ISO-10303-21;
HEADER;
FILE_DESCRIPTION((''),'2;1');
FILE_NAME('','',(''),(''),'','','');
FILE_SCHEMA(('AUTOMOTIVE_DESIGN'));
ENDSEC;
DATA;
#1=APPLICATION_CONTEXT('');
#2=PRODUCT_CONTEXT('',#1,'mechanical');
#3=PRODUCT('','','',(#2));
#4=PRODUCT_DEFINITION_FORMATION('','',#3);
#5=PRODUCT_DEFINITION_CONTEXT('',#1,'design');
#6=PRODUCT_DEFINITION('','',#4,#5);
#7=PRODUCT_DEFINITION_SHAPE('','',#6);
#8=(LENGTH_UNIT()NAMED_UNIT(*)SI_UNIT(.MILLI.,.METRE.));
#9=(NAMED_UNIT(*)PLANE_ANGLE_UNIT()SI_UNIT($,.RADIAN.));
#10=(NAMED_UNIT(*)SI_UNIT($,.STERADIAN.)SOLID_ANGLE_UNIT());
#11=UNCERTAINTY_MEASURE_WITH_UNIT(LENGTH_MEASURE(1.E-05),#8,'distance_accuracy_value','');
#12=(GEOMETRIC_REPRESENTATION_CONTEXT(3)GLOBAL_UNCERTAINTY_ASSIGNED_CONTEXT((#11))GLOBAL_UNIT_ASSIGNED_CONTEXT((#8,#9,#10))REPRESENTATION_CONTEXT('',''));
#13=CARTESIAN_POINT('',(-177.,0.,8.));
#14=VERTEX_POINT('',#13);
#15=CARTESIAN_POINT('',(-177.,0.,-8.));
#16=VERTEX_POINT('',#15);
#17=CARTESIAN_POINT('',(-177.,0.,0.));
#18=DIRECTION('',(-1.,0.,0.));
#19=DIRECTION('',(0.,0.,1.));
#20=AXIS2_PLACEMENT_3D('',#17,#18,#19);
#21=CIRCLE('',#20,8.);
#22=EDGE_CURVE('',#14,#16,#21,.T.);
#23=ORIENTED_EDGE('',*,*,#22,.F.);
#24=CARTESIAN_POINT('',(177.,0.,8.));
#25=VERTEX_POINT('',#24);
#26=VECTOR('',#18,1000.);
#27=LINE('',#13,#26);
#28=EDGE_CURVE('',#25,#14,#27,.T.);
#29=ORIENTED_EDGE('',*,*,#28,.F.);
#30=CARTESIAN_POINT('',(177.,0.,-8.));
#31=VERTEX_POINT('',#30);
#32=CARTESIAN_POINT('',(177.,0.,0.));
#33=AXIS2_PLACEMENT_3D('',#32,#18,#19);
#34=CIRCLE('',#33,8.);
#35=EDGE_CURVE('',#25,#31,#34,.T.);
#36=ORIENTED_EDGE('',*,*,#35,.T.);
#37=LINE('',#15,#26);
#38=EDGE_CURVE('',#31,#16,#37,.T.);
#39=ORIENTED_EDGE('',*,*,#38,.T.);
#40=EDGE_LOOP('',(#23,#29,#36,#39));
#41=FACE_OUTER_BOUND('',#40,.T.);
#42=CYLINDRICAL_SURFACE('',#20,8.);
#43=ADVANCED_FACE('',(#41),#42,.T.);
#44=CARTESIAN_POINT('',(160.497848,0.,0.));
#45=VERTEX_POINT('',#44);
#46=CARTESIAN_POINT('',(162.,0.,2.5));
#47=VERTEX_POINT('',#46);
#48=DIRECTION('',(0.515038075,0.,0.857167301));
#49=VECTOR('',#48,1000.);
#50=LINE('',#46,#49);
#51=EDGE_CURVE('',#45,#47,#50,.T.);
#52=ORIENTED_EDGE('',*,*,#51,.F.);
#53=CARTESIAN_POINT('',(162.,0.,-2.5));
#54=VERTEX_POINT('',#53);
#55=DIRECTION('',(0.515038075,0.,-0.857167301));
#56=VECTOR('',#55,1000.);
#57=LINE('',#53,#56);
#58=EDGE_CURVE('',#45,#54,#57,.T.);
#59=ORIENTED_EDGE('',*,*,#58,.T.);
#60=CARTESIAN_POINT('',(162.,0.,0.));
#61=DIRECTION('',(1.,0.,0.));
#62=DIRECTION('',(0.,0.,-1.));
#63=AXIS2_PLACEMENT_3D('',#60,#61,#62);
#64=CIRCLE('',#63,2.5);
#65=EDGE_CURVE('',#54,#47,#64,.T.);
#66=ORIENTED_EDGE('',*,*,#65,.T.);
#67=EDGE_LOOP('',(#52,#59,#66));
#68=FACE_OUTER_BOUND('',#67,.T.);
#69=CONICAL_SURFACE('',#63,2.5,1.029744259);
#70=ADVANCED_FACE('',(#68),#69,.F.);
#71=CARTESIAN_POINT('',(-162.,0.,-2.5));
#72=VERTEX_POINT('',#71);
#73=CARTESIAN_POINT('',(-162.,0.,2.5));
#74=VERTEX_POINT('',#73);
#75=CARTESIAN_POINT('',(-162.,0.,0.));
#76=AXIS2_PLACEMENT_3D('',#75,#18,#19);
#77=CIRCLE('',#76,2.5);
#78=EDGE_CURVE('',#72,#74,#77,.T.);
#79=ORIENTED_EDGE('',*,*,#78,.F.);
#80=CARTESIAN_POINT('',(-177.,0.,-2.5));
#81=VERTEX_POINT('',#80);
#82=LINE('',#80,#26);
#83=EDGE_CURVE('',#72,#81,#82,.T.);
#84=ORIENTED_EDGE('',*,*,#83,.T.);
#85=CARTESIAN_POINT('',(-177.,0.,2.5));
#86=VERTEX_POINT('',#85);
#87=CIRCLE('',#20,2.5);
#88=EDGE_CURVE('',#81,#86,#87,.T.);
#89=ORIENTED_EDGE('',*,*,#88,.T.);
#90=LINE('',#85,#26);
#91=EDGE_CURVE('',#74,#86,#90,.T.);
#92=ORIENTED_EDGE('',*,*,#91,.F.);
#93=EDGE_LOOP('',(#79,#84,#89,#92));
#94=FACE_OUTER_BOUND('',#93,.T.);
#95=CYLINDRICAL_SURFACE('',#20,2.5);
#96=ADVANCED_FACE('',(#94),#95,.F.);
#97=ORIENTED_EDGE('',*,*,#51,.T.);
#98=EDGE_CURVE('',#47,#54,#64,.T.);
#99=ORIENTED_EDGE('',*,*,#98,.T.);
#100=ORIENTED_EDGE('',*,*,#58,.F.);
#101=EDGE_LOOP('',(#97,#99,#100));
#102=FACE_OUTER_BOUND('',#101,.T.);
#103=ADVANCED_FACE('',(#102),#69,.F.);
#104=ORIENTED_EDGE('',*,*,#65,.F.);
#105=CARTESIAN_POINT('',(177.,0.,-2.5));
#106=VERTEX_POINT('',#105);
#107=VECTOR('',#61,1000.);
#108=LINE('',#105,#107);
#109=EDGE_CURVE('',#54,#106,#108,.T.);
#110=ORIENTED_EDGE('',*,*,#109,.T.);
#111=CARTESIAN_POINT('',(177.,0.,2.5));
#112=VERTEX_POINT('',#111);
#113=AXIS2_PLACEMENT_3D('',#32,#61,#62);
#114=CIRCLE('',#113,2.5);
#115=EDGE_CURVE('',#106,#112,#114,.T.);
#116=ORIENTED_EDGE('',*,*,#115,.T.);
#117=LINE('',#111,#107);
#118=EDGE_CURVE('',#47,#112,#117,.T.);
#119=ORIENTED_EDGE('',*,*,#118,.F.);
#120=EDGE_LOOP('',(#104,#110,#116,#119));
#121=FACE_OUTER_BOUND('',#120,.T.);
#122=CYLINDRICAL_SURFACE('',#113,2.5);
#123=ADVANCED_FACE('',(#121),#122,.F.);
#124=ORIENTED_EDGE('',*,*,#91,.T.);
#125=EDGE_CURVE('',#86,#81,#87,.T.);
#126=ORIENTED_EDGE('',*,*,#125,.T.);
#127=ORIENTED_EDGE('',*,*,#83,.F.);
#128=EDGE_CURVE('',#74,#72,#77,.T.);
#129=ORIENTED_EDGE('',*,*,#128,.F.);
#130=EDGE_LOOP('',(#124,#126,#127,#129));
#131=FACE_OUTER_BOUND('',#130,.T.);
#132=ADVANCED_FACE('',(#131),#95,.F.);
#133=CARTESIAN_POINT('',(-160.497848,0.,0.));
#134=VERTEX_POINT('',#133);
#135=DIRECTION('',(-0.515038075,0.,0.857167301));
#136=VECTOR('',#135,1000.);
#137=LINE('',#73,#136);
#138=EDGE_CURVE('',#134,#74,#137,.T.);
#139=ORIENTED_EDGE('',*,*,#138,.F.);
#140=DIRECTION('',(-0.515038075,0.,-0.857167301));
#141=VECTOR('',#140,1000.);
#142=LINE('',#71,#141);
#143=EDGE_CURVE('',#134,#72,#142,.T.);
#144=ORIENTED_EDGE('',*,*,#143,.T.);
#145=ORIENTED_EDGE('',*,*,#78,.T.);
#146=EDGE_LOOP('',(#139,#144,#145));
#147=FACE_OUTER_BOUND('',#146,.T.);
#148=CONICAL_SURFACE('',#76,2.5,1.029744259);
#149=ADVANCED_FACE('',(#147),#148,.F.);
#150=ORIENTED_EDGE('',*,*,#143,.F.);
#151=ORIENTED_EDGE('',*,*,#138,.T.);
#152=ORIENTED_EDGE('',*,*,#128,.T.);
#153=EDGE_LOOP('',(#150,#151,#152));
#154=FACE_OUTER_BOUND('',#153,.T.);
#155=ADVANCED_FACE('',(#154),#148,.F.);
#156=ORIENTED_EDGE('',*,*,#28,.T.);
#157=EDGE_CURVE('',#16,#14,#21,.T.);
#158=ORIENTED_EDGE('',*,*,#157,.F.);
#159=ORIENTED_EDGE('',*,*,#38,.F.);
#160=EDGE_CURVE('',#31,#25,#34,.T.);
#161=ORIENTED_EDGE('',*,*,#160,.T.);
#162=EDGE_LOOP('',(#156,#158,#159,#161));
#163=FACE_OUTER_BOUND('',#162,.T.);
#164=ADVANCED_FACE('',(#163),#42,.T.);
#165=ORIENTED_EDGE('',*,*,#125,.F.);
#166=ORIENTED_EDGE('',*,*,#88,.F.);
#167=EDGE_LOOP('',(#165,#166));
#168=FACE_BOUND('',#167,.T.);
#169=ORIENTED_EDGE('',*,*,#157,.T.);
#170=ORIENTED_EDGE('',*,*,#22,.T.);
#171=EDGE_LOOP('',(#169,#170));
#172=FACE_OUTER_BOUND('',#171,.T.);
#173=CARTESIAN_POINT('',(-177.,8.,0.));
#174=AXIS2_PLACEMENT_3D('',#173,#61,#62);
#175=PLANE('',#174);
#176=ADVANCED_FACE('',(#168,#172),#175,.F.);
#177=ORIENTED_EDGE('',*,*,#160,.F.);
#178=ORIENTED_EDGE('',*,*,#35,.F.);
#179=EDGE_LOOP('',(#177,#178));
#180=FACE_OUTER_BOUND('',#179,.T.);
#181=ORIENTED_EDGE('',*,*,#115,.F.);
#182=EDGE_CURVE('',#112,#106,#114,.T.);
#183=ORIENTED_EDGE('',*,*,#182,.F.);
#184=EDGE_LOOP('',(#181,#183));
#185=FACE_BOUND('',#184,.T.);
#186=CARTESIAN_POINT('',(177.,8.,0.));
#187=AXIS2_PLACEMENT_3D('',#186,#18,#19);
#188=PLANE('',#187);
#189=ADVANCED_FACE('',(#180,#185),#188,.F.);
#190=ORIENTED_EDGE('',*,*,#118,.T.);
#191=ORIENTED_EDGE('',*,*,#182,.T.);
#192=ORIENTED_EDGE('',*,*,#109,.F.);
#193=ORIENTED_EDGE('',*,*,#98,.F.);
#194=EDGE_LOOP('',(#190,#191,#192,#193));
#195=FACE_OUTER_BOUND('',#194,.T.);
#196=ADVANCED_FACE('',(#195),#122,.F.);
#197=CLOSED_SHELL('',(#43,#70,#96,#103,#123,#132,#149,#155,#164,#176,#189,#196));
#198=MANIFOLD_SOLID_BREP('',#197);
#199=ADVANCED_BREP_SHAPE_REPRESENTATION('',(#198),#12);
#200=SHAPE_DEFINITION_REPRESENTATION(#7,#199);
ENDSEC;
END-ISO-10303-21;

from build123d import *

# Parameters (mm, degrees)
SKETCH1_W             = 354
SKETCH1_H             = 8
M6_TAPPED_HOLE1_D     = 5
M6_TAPPED_HOLE1_DEPTH = 15
M6_TAPPED_HOLE1_TIP   = 1.502151548
M6_TAPPED_HOLE2_D     = 5
M6_TAPPED_HOLE2_DEPTH = 15
M6_TAPPED_HOLE2_TIP   = 1.502151548


with BuildPart() as part:
    # Sketch1 → Revolve1 (revolve)
    with BuildSketch(Plane.XY, mode=Mode.PRIVATE) as revolve1_sk:
        with Locations((0, 4)):
            Rectangle(SKETCH1_W, SKETCH1_H)
    revolve(revolve1_sk.sketch.rotate(Axis((-177, 0, 0), (1, 0, 0)), 90), axis=Axis((-177, 0, 0), (1, 0, 0)))

    # M6 Tapped Hole1
    with Locations(Plane(origin=(177, 0, 0), x_dir=(0, 0, -1), z_dir=(1, 0, 0))):
        with Locations((0, 0)):
            Hole(M6_TAPPED_HOLE1_D / 2, depth=M6_TAPPED_HOLE1_DEPTH)
            with Locations((0, 0, -(M6_TAPPED_HOLE1_DEPTH + M6_TAPPED_HOLE1_TIP / 2))):  # 118° drill point
                Cone(0, M6_TAPPED_HOLE1_D / 2, M6_TAPPED_HOLE1_TIP, mode=Mode.SUBTRACT)

    # M6 Tapped Hole2
    with Locations(Plane.ZY.offset(177)):
        with Locations((0, 0)):
            Hole(M6_TAPPED_HOLE2_D / 2, depth=M6_TAPPED_HOLE2_DEPTH)
            with Locations((0, 0, -(M6_TAPPED_HOLE2_DEPTH + M6_TAPPED_HOLE2_TIP / 2))):  # 118° drill point
                Cone(0, M6_TAPPED_HOLE2_D / 2, M6_TAPPED_HOLE2_TIP, mode=Mode.SUBTRACT)


solid = part.part
